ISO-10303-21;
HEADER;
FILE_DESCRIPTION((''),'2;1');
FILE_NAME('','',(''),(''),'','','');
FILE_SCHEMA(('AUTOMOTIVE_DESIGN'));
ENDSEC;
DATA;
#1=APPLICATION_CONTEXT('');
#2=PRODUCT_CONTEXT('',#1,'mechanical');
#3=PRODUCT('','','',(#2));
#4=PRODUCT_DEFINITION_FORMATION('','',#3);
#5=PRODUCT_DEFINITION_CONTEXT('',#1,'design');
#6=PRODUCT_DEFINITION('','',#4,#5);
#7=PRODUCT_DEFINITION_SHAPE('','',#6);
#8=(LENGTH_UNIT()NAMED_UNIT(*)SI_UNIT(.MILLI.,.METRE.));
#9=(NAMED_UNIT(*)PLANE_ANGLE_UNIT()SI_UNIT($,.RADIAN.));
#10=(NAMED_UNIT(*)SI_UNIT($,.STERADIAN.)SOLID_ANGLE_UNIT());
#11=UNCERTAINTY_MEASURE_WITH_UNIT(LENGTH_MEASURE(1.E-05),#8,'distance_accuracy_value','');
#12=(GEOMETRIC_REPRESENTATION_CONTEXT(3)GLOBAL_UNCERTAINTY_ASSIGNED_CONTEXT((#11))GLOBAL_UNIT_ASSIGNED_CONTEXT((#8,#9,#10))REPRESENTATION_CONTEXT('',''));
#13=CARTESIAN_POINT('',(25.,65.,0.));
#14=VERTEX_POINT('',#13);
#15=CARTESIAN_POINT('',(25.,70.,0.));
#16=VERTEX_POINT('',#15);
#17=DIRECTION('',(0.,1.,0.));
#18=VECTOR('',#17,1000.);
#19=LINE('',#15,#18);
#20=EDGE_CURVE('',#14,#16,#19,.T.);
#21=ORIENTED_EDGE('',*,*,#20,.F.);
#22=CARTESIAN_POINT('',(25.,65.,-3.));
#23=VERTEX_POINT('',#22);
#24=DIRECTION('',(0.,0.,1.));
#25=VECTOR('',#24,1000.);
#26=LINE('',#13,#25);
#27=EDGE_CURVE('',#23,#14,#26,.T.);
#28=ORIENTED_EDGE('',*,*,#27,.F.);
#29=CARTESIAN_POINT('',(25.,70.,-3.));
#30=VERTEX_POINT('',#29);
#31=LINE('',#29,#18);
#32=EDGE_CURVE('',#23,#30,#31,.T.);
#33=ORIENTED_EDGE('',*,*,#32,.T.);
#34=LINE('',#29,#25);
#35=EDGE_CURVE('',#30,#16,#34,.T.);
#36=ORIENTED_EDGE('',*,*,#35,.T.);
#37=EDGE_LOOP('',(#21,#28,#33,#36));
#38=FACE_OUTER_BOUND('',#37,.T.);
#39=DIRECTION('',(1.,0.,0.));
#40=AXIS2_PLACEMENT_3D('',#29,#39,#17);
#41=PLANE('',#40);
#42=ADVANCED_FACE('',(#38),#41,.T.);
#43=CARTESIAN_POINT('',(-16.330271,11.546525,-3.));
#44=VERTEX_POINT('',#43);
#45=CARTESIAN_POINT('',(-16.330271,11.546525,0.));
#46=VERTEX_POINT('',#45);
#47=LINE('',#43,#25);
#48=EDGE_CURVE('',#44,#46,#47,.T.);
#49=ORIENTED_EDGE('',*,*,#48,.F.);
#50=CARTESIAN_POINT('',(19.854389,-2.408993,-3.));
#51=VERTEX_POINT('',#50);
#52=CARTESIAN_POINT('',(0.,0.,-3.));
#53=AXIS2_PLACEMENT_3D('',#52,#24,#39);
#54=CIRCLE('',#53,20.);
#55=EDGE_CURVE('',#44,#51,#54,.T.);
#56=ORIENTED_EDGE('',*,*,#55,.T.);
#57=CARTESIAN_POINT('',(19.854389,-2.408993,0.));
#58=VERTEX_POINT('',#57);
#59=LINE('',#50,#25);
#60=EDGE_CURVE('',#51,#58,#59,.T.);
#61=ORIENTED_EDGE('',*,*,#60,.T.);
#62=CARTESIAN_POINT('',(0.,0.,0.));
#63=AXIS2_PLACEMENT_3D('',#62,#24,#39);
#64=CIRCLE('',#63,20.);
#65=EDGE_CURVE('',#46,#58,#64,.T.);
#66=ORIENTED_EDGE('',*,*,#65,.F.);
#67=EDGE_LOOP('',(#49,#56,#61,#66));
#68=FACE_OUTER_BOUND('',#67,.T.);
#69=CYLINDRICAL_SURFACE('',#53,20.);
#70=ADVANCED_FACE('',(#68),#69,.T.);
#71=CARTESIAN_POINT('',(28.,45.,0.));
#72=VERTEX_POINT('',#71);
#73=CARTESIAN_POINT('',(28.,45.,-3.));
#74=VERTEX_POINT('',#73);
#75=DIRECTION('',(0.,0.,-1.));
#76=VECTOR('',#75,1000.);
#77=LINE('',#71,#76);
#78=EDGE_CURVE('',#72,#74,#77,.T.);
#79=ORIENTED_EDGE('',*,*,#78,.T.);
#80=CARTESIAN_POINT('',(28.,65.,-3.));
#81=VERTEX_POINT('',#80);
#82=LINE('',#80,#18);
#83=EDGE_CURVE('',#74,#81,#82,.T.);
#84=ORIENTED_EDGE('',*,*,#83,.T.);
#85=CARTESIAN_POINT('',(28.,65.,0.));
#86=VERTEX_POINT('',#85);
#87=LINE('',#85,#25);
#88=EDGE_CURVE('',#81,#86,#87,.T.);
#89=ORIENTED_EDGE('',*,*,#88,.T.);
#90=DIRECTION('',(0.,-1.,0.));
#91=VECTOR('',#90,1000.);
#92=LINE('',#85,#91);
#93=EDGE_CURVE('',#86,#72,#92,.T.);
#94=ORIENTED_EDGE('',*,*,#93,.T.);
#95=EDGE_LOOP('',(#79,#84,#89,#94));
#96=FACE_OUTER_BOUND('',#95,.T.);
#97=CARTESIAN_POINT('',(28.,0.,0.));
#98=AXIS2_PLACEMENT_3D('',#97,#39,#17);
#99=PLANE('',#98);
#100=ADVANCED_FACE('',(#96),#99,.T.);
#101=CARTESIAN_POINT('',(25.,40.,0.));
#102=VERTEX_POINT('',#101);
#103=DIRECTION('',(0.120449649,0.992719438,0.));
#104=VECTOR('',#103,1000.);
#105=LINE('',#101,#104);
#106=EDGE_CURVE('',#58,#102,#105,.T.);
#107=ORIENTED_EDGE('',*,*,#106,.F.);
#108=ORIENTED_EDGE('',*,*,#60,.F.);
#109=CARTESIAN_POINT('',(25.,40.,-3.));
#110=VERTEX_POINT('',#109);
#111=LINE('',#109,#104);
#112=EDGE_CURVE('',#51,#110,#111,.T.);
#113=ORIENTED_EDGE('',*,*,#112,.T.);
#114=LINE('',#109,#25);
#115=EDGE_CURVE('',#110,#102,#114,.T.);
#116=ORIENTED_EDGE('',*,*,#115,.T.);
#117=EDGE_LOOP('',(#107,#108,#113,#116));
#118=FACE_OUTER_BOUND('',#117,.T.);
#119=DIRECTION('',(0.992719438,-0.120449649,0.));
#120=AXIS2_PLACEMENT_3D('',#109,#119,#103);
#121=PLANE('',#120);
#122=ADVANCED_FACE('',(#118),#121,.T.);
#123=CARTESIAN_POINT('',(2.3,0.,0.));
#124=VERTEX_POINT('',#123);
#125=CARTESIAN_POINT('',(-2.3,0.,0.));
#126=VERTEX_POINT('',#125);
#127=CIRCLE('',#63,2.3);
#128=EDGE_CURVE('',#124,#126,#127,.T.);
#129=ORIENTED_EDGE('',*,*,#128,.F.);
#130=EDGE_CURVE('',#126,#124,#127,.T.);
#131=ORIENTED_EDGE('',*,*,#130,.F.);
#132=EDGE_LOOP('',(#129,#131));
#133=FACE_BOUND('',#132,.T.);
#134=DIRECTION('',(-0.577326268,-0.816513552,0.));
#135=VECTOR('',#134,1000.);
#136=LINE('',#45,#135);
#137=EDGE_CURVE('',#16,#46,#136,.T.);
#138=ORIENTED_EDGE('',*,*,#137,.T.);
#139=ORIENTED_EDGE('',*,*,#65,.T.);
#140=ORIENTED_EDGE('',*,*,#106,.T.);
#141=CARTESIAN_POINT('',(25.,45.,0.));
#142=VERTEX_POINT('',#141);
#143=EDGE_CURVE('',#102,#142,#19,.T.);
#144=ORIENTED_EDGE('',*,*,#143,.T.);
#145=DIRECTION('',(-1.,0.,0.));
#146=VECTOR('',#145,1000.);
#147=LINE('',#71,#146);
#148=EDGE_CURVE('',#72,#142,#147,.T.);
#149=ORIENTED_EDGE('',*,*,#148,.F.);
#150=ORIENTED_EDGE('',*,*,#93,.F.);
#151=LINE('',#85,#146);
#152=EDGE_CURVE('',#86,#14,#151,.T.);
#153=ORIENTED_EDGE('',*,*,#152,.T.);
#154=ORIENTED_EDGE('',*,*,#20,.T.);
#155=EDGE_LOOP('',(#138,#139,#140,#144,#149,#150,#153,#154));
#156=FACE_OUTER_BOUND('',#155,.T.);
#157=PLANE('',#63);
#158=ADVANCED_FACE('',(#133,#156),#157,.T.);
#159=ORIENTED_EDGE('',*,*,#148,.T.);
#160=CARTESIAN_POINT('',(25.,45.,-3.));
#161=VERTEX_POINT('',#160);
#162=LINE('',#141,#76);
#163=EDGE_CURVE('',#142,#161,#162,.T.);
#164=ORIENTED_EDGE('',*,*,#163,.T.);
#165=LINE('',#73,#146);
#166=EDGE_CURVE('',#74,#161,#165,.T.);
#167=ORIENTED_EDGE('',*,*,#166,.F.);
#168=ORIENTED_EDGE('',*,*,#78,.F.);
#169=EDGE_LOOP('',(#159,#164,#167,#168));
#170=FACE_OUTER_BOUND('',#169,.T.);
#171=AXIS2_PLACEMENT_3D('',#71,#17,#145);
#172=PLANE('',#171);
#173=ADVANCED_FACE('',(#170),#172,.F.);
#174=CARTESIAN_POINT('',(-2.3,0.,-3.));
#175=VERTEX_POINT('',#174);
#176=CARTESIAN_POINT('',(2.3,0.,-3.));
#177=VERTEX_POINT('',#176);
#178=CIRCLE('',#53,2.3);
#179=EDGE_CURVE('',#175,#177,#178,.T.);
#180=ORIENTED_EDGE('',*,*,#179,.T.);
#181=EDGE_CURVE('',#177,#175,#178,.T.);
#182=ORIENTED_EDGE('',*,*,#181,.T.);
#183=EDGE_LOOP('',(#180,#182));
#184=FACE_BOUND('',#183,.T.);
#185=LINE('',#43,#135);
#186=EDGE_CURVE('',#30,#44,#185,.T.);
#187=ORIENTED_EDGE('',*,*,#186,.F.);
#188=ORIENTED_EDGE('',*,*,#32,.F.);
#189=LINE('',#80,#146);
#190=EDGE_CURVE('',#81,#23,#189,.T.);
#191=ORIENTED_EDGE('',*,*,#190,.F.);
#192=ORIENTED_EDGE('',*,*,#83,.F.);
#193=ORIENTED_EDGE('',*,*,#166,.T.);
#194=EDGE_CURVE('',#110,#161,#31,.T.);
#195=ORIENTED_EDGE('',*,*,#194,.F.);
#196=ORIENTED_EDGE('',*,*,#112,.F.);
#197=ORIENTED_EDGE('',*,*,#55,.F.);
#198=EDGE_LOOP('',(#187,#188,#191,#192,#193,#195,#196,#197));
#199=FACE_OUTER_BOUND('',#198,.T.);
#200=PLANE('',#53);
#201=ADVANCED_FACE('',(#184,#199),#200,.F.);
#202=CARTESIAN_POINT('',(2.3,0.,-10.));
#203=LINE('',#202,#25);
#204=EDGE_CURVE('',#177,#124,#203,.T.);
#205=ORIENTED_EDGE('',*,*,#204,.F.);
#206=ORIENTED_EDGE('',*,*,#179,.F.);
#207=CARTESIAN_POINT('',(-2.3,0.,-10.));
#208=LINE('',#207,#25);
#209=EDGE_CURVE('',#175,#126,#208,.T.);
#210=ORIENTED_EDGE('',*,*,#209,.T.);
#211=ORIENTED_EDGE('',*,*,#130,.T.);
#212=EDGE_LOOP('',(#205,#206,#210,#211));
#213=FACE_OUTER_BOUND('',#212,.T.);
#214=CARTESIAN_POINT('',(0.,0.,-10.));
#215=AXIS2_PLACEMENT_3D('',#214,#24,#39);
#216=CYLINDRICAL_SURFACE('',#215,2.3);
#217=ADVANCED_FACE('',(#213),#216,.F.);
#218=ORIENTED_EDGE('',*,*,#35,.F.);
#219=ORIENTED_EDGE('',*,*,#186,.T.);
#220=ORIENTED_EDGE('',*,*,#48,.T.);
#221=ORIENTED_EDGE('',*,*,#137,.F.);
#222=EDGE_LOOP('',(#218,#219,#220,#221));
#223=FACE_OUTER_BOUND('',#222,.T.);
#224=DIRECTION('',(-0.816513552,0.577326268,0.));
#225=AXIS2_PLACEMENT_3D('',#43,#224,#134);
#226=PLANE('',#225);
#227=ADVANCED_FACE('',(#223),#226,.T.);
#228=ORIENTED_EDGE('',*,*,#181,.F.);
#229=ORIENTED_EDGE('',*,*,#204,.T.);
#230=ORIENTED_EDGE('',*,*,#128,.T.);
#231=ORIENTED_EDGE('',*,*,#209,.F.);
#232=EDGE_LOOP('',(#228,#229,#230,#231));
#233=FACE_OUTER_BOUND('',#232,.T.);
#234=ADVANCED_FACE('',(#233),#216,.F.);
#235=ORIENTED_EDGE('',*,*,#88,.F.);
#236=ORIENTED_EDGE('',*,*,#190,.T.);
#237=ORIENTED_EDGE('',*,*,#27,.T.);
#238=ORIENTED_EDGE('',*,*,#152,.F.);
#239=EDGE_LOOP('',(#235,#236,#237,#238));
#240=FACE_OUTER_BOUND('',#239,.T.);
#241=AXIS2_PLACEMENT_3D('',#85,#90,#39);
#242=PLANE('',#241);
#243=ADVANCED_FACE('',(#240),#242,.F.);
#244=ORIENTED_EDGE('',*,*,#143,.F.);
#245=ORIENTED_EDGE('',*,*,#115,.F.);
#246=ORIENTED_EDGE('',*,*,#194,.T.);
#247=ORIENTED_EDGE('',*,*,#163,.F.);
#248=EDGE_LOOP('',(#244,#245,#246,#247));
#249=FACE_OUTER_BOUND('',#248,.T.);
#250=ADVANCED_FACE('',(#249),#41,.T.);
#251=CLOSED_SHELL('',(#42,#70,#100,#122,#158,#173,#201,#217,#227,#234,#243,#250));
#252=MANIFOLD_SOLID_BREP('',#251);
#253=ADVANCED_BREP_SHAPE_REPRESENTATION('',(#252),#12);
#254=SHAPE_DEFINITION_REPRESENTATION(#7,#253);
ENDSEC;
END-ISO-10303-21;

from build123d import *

# Parameters (mm, degrees)
BOSS_EXTRUDE1_DEPTH = 3
SKETCH2_R           = 2.3
CUT_EXTRUDE1_DEPTH  = 10
SKETCH4_W           = 3
SKETCH4_H           = 20
BOSS_EXTRUDE3_DEPTH = 3


with BuildPart() as part:
    # Sketch1 → Boss-Extrude1 (new body)
    with BuildSketch(Plane.XY):
        with BuildLine():
            Line((-16.33027103, 11.546525368), (25, 70))
            Line((25, 70), (25, 40))
            Line((25, 40), (19.854388756, -2.408992972))
            ThreePointArc((19.854388756, -2.408992972), (-7.196803073, -18.660279353), (-16.33027103, 11.546525368))
        make_face()
    extrude(amount=-BOSS_EXTRUDE1_DEPTH)

    # Sketch2 → Cut-Extrude1 (cut)
    with BuildSketch(Plane.XY):
        Circle(SKETCH2_R)
    extrude(amount=-CUT_EXTRUDE1_DEPTH, mode=Mode.SUBTRACT)

    # Sketch4 → Boss-Extrude3 (add)
    with BuildSketch(Plane(origin=(25, 0, 0), x_dir=(0, 0, -1), z_dir=(1, 0, 0))):
        with Locations((1.5, 55)):
            Rectangle(SKETCH4_W, SKETCH4_H)
    extrude(amount=BOSS_EXTRUDE3_DEPTH)


solid = part.part
